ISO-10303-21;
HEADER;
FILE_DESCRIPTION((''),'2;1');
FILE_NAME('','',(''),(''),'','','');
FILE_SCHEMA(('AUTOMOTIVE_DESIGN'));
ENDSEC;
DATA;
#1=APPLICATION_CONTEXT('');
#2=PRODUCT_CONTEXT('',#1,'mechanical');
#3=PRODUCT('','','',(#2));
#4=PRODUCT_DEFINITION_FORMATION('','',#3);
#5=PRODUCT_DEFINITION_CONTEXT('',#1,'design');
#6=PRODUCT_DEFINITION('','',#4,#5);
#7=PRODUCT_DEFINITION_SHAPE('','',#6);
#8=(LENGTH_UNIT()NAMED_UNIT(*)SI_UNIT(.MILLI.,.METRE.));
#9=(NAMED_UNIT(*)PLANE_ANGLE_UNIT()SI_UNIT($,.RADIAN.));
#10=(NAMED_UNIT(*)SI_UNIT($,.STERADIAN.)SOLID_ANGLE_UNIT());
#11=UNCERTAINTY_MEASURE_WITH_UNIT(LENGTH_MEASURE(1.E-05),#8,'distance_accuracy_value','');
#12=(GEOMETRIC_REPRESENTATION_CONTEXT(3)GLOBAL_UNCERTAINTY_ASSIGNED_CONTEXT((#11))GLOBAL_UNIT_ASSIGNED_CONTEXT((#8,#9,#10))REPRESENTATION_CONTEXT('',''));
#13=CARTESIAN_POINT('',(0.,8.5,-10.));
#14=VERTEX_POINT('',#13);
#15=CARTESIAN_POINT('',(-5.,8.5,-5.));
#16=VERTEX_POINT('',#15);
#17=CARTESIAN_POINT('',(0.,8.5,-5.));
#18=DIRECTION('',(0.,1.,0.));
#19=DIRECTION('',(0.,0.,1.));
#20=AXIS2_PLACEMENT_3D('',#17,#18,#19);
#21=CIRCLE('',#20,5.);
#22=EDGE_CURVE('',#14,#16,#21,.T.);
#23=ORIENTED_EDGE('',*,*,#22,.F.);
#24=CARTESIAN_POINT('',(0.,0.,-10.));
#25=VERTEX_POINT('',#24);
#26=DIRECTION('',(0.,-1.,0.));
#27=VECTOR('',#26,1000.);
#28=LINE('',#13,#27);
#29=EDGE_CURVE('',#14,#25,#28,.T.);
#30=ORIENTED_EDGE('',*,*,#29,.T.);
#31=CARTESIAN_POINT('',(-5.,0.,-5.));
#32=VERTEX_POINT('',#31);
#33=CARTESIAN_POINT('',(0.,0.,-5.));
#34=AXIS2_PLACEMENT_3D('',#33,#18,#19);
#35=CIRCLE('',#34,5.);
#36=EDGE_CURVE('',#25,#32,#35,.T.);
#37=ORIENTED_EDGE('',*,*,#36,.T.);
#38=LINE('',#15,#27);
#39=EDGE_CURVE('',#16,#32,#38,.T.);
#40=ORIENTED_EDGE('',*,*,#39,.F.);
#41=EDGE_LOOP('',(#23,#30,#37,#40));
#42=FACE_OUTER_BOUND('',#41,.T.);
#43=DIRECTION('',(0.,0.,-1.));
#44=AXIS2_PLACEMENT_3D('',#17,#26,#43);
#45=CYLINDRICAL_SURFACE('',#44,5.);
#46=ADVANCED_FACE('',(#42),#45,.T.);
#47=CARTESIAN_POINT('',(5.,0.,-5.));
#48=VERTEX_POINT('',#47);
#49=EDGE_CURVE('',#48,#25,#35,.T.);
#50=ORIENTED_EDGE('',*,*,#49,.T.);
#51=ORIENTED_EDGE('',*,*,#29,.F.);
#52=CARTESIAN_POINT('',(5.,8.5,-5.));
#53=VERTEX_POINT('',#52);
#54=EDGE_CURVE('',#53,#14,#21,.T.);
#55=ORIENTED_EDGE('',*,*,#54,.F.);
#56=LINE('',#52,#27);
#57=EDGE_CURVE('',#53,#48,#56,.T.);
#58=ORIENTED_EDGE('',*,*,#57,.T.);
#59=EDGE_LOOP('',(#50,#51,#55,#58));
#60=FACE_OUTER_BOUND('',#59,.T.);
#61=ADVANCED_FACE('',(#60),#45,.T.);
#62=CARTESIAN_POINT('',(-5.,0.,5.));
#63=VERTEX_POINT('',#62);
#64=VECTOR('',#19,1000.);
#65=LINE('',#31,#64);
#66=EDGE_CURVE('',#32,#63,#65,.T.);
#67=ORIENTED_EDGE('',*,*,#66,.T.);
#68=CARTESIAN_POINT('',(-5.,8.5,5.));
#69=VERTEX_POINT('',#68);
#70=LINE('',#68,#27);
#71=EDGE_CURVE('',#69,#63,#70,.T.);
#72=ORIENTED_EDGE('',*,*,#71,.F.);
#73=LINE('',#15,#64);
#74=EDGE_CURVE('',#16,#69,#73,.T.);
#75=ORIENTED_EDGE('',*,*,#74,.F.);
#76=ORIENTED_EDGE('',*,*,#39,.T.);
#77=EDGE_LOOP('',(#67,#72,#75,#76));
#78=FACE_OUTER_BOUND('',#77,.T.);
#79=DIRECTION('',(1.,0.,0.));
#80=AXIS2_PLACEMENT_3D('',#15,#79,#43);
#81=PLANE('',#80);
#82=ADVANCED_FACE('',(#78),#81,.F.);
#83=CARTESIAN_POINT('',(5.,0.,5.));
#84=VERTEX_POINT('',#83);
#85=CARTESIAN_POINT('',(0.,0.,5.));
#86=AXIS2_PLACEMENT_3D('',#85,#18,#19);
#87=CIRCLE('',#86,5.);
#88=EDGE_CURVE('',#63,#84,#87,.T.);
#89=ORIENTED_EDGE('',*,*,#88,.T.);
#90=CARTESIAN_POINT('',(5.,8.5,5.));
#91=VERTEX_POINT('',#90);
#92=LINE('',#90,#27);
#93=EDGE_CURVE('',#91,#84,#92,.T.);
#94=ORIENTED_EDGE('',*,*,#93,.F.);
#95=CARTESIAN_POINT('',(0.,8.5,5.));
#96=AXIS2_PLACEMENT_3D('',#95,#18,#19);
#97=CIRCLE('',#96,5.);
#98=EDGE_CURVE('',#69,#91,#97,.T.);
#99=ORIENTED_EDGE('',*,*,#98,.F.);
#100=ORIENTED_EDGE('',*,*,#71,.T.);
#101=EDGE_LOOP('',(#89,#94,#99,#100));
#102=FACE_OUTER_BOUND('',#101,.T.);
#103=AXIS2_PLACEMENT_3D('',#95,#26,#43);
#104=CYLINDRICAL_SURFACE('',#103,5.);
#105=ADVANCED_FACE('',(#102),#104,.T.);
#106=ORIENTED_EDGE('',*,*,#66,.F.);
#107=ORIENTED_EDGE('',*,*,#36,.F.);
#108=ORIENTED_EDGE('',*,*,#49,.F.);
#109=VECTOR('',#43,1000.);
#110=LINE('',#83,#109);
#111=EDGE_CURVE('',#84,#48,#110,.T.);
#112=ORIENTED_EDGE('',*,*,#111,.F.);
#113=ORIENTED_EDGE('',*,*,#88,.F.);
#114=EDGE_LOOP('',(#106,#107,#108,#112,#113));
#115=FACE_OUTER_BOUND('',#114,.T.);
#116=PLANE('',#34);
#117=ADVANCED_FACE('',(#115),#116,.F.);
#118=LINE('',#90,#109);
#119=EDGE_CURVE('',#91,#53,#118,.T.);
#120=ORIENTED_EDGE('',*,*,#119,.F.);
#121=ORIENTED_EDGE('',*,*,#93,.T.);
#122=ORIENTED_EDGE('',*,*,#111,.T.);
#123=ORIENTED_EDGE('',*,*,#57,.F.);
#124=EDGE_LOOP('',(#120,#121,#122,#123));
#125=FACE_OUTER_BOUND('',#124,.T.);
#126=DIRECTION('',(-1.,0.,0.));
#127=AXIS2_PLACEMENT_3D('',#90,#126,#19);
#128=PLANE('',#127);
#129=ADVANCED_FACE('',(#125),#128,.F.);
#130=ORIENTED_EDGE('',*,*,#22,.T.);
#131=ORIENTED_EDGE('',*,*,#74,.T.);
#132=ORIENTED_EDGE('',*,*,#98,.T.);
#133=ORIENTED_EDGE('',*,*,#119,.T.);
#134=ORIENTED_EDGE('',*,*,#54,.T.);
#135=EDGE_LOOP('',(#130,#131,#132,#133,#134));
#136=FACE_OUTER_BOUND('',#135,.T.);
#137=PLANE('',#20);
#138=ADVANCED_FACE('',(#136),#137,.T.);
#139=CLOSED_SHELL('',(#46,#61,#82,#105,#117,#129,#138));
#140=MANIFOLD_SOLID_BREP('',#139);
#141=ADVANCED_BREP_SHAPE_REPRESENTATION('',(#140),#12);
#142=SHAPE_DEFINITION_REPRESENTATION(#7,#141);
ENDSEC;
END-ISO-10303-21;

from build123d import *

# Parameters (mm, degrees)
BOSS_EXTRUDE1_DEPTH = 8.5


with BuildPart() as part:
    # Sketch1 → Boss-Extrude1 (new body)
    with BuildSketch(Plane(origin=(0, 0, 0), x_dir=(1, 0, 0), z_dir=(0, 1, 0))):
        with BuildLine():
            Line((-5, 5), (-5, -5))
            ThreePointArc((-5, -5), (0, -10), (5, -5))
            Line((5, -5), (5, 5))
            ThreePointArc((5, 5), (0, 10), (-5, 5))
        make_face()
    extrude(amount=BOSS_EXTRUDE1_DEPTH)


solid = part.part
